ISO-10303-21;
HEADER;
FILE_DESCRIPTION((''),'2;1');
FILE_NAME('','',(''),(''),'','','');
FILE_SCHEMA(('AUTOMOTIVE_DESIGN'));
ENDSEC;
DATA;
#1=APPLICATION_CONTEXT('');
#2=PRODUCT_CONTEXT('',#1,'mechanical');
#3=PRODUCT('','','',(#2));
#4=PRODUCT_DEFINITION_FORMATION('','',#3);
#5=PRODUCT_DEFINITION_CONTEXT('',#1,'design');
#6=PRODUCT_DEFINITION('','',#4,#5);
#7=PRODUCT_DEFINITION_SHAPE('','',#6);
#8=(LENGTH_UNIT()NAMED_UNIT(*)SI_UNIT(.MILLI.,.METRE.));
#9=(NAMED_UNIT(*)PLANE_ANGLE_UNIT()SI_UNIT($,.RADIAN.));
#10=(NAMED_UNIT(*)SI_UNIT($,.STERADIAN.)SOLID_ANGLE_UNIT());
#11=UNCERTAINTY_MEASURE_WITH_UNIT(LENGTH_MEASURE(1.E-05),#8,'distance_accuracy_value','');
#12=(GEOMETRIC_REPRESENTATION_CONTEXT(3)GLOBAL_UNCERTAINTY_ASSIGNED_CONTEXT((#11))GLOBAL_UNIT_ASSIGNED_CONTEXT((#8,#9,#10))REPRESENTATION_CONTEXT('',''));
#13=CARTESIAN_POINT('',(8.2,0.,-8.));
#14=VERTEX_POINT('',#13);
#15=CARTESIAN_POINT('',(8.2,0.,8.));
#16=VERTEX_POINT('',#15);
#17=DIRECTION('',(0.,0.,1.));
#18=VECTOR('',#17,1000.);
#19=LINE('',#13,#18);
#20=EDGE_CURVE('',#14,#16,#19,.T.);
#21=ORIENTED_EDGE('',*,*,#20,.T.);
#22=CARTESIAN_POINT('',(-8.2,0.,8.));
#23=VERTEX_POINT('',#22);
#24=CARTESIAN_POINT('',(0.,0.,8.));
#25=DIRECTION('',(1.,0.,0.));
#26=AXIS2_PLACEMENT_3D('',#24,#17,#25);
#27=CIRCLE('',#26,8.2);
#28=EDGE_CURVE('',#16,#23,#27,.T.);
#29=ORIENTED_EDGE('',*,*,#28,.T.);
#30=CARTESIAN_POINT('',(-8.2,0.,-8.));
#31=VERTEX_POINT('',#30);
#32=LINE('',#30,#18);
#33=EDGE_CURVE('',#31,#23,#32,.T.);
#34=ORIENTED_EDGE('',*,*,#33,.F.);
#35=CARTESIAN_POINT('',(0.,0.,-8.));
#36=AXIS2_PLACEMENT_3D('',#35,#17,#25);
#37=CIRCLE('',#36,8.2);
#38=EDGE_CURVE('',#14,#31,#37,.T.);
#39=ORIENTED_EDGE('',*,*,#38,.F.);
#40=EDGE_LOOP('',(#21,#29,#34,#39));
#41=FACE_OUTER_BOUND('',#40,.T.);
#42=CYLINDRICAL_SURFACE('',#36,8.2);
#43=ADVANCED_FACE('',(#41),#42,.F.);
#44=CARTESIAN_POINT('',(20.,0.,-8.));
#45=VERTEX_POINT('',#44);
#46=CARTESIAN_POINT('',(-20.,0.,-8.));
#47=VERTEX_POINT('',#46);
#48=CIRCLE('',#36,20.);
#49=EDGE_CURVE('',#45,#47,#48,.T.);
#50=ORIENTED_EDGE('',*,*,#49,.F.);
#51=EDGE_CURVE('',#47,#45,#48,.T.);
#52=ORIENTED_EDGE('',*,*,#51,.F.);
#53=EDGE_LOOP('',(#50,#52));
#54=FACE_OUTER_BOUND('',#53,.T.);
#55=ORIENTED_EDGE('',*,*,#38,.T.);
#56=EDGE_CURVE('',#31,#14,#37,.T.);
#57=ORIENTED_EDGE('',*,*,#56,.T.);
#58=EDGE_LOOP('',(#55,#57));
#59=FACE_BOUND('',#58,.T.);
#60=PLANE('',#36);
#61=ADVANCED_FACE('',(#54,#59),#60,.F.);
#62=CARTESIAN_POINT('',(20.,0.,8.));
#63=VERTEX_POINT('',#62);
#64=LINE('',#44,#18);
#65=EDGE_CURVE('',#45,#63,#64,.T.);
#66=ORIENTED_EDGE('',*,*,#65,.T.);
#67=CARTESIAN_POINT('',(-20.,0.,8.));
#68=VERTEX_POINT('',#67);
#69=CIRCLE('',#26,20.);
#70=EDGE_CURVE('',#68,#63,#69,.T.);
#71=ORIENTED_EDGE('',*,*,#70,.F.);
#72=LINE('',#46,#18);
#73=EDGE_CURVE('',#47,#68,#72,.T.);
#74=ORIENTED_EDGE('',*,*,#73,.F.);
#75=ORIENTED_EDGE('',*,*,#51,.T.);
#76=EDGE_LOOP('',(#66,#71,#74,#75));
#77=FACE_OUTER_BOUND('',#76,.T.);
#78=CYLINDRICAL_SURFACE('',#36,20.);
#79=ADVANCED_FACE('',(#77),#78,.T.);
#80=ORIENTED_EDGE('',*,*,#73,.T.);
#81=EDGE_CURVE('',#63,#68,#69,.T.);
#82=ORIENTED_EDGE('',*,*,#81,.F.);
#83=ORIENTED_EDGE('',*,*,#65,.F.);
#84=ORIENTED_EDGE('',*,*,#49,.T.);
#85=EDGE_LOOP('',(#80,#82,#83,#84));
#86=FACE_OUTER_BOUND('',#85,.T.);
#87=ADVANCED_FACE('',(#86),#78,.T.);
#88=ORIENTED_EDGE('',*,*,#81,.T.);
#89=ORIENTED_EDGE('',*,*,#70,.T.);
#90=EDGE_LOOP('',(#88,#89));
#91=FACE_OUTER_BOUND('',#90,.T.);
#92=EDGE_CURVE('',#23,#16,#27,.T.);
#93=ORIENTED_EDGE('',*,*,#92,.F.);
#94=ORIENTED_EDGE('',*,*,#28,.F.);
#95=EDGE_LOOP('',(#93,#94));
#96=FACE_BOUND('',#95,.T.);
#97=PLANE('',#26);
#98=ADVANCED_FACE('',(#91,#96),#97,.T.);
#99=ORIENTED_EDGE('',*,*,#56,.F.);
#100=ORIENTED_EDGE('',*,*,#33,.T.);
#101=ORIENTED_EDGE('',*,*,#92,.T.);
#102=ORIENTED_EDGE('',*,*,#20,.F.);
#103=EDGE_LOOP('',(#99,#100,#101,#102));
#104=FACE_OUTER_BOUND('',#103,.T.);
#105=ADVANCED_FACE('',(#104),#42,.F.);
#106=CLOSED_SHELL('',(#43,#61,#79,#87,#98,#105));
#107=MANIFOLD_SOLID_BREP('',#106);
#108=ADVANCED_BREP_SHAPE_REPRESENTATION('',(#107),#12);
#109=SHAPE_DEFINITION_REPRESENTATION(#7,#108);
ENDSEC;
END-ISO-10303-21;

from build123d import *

# Parameters (mm, degrees)
SKETCH_1_R      = 20
SKETCH_1_R_2    = 8.2
EXTRUDE_1_DEPTH = 8


with BuildPart() as part:
    # 草图1 → 凸台-拉伸1 (new, symmetric)
    with BuildSketch(Plane.XY):
        Circle(SKETCH_1_R)
        Circle(SKETCH_1_R_2, mode=Mode.SUBTRACT)
    extrude(amount=EXTRUDE_1_DEPTH, both=True)


solid = part.part
